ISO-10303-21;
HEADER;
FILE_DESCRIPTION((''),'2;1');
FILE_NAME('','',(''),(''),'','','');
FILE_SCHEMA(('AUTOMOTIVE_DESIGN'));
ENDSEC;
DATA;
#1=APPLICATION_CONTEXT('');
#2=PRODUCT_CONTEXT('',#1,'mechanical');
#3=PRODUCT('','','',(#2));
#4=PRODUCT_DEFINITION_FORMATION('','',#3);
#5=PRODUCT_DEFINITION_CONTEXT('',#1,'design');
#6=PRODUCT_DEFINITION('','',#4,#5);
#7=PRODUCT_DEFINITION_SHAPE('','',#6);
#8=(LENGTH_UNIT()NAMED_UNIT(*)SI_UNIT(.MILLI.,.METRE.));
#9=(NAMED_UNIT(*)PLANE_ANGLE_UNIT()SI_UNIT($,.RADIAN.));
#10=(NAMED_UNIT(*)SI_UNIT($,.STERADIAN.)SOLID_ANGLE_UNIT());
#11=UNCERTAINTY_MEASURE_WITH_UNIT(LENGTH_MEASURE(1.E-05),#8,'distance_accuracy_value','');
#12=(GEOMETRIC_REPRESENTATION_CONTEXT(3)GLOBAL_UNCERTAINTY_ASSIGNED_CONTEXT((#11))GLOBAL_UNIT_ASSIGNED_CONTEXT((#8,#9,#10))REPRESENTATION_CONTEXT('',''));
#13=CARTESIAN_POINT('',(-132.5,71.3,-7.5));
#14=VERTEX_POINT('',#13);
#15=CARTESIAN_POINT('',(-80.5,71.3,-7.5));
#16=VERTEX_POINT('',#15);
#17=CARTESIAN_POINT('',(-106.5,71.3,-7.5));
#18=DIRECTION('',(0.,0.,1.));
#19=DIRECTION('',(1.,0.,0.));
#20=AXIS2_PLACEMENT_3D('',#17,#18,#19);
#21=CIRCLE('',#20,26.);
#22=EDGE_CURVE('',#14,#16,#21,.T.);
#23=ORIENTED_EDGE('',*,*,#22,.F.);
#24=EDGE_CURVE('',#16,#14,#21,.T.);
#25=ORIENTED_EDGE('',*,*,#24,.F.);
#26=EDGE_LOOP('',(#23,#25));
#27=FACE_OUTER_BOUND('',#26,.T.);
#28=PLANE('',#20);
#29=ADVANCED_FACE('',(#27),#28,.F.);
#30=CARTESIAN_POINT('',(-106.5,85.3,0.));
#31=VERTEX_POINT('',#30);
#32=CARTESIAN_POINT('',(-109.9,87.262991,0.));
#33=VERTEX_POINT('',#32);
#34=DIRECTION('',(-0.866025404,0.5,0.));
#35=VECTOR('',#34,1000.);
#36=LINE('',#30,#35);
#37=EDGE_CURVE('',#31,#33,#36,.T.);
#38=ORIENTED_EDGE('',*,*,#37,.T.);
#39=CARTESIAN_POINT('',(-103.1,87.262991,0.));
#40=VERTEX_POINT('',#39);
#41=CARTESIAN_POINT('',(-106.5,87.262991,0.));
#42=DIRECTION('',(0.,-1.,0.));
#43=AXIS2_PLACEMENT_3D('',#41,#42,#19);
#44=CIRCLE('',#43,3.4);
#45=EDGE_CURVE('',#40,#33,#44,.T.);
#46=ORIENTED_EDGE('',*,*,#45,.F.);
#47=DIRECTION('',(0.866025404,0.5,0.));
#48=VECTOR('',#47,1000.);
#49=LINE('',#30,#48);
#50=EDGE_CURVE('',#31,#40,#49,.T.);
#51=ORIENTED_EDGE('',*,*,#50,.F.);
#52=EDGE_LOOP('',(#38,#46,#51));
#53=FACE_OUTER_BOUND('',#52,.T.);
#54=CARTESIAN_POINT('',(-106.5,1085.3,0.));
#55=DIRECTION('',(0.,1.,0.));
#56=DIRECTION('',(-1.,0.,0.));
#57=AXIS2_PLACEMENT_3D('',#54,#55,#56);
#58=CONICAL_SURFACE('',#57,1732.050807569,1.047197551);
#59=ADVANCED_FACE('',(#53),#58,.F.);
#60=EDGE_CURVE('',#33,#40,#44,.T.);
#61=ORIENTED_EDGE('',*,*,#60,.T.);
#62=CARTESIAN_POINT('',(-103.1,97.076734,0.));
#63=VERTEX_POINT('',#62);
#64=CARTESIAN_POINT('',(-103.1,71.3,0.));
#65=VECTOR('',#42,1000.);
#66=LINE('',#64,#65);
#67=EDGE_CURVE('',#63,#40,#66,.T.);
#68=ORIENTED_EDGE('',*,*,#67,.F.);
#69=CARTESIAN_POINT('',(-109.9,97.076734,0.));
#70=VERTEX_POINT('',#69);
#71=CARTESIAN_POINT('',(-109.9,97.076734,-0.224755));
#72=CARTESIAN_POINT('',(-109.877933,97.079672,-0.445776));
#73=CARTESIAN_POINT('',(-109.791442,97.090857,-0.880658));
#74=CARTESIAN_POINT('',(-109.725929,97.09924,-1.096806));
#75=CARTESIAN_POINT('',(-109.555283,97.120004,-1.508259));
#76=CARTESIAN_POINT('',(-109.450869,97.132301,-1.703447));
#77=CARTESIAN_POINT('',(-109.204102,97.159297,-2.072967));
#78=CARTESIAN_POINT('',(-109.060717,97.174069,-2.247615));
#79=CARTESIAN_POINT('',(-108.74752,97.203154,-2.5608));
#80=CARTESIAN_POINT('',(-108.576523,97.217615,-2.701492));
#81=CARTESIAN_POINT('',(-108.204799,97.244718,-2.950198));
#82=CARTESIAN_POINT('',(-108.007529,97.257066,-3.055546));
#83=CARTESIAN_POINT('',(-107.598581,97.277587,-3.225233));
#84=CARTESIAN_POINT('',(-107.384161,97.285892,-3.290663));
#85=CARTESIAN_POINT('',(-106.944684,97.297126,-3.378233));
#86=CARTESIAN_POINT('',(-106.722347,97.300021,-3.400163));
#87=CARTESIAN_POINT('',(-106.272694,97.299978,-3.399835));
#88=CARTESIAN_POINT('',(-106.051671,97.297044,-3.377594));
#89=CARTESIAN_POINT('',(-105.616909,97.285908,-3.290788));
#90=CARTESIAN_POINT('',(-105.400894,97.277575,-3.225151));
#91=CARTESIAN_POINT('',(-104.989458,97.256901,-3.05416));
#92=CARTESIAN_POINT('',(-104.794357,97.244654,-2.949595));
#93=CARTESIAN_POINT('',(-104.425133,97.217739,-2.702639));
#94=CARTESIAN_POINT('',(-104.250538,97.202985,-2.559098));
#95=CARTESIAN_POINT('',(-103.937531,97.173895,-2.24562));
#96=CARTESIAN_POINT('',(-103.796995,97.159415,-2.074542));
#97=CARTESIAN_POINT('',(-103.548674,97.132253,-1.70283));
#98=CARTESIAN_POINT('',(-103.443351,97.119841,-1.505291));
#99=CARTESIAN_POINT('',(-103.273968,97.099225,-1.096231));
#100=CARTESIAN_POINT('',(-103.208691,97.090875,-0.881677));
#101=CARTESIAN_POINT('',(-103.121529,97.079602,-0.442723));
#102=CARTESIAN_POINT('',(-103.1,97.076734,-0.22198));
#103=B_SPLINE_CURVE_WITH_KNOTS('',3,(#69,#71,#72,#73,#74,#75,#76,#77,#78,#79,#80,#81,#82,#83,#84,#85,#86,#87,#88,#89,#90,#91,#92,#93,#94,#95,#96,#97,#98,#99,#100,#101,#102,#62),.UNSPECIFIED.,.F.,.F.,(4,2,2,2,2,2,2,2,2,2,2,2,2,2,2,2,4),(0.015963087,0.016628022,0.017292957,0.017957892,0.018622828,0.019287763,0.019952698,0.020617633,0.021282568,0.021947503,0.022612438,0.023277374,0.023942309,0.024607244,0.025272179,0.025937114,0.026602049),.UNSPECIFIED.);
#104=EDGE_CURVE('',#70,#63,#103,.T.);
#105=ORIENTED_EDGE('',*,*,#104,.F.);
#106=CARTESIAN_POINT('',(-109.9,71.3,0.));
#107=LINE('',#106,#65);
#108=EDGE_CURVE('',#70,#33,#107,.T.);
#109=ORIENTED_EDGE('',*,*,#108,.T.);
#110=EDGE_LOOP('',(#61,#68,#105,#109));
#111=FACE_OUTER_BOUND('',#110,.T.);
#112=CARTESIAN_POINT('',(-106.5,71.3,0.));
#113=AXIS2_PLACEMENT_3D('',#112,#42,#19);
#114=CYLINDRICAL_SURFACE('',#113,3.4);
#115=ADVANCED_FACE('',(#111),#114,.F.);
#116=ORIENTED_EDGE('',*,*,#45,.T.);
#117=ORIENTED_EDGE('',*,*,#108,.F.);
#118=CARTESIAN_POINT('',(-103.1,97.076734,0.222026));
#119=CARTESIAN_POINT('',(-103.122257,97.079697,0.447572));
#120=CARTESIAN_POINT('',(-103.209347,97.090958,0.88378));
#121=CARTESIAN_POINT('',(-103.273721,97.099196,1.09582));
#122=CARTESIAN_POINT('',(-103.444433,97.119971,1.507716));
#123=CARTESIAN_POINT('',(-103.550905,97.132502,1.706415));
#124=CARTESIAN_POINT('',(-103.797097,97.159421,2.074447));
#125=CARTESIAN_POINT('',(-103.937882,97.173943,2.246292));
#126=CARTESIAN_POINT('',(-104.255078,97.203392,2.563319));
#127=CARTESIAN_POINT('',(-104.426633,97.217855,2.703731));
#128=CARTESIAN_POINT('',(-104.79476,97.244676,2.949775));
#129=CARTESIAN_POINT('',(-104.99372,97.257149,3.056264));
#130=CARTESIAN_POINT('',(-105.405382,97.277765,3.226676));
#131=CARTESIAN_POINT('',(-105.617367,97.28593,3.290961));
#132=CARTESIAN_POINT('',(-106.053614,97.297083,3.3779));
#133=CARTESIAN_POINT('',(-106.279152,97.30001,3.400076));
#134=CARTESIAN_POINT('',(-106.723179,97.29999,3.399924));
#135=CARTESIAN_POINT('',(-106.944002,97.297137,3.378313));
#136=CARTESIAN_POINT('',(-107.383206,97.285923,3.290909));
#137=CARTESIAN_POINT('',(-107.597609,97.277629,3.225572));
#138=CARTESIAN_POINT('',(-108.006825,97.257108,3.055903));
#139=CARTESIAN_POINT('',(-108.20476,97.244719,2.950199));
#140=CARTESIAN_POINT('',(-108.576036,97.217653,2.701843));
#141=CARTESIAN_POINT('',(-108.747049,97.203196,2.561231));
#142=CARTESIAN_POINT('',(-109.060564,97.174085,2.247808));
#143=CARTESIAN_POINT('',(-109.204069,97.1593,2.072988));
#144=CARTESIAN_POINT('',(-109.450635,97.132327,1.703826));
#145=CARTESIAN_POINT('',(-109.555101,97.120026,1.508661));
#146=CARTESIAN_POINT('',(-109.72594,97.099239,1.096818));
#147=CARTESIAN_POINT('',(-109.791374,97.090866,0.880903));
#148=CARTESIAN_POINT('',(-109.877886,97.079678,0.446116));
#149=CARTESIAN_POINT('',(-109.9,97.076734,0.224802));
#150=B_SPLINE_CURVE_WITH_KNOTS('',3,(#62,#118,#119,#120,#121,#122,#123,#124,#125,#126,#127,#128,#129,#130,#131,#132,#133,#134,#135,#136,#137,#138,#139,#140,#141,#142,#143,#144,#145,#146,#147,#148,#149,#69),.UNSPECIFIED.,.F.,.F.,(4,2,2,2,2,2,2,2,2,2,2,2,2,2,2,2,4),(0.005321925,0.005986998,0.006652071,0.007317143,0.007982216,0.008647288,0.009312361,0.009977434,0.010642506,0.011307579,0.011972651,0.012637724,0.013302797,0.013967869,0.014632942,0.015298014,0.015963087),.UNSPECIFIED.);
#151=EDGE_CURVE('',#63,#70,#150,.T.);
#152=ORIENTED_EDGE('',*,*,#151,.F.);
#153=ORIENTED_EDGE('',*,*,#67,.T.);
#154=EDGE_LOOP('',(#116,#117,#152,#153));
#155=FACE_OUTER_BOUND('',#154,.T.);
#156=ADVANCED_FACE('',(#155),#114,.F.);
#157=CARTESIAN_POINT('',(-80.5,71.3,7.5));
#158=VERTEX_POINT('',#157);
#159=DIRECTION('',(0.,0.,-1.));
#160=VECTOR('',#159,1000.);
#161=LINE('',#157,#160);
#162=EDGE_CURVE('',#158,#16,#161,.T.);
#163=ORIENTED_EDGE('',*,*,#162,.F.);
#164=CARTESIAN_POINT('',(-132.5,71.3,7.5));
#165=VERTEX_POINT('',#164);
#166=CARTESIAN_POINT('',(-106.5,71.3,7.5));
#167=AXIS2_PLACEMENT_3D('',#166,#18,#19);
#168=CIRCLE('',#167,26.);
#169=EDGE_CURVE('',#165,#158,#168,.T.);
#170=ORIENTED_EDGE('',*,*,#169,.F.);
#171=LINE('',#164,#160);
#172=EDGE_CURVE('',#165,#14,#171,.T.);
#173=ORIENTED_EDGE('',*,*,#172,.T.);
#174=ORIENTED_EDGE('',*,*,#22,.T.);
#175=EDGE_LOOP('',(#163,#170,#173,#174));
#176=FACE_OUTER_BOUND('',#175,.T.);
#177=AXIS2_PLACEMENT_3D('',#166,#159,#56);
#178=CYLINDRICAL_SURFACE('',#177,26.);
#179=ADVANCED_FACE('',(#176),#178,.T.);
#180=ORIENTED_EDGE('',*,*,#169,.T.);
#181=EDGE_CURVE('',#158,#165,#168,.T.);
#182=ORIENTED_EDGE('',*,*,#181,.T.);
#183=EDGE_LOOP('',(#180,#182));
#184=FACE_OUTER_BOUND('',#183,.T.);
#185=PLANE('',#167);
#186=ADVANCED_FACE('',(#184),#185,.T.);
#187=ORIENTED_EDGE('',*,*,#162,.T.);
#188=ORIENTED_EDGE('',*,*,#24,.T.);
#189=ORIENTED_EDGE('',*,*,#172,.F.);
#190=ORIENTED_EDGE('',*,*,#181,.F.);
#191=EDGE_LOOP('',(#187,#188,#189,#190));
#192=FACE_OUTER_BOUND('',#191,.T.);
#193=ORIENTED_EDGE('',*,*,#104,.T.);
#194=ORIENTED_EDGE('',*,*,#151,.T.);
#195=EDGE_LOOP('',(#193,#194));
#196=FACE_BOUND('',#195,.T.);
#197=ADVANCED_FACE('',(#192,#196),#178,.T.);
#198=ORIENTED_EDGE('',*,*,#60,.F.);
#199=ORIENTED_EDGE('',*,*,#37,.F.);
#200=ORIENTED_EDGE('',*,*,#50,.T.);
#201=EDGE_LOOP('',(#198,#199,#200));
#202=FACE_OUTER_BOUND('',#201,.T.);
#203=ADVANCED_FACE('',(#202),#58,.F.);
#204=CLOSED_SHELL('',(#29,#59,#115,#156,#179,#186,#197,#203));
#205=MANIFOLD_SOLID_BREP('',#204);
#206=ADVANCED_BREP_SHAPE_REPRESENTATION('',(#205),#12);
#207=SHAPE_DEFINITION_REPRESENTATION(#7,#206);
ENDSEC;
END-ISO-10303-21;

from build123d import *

# Parameters (mm, degrees)
SKETCH1_R           = 26
BOSS_EXTRUDE1_DEPTH = 7.5


with BuildPart() as part:
    # Sketch1 → Boss-Extrude1 (new, symmetric)
    with BuildSketch(Plane.XY):
        with Locations((-106.5, 71.3)):
            Circle(SKETCH1_R)
    extrude(amount=BOSS_EXTRUDE1_DEPTH, both=True)

    # Sketch2 → Cut-Revolve1 (revolve, cut)
    with BuildSketch(Plane.XY):
        Polygon((-106.5, 97.3), (-103.1, 97.3), (-103.1, 87.262990915), (-106.5, 85.3), align=None)
    revolve(axis=Axis((-106.5, 71.3, 0), (0, 1, 0)), mode=Mode.SUBTRACT)


solid = part.part
